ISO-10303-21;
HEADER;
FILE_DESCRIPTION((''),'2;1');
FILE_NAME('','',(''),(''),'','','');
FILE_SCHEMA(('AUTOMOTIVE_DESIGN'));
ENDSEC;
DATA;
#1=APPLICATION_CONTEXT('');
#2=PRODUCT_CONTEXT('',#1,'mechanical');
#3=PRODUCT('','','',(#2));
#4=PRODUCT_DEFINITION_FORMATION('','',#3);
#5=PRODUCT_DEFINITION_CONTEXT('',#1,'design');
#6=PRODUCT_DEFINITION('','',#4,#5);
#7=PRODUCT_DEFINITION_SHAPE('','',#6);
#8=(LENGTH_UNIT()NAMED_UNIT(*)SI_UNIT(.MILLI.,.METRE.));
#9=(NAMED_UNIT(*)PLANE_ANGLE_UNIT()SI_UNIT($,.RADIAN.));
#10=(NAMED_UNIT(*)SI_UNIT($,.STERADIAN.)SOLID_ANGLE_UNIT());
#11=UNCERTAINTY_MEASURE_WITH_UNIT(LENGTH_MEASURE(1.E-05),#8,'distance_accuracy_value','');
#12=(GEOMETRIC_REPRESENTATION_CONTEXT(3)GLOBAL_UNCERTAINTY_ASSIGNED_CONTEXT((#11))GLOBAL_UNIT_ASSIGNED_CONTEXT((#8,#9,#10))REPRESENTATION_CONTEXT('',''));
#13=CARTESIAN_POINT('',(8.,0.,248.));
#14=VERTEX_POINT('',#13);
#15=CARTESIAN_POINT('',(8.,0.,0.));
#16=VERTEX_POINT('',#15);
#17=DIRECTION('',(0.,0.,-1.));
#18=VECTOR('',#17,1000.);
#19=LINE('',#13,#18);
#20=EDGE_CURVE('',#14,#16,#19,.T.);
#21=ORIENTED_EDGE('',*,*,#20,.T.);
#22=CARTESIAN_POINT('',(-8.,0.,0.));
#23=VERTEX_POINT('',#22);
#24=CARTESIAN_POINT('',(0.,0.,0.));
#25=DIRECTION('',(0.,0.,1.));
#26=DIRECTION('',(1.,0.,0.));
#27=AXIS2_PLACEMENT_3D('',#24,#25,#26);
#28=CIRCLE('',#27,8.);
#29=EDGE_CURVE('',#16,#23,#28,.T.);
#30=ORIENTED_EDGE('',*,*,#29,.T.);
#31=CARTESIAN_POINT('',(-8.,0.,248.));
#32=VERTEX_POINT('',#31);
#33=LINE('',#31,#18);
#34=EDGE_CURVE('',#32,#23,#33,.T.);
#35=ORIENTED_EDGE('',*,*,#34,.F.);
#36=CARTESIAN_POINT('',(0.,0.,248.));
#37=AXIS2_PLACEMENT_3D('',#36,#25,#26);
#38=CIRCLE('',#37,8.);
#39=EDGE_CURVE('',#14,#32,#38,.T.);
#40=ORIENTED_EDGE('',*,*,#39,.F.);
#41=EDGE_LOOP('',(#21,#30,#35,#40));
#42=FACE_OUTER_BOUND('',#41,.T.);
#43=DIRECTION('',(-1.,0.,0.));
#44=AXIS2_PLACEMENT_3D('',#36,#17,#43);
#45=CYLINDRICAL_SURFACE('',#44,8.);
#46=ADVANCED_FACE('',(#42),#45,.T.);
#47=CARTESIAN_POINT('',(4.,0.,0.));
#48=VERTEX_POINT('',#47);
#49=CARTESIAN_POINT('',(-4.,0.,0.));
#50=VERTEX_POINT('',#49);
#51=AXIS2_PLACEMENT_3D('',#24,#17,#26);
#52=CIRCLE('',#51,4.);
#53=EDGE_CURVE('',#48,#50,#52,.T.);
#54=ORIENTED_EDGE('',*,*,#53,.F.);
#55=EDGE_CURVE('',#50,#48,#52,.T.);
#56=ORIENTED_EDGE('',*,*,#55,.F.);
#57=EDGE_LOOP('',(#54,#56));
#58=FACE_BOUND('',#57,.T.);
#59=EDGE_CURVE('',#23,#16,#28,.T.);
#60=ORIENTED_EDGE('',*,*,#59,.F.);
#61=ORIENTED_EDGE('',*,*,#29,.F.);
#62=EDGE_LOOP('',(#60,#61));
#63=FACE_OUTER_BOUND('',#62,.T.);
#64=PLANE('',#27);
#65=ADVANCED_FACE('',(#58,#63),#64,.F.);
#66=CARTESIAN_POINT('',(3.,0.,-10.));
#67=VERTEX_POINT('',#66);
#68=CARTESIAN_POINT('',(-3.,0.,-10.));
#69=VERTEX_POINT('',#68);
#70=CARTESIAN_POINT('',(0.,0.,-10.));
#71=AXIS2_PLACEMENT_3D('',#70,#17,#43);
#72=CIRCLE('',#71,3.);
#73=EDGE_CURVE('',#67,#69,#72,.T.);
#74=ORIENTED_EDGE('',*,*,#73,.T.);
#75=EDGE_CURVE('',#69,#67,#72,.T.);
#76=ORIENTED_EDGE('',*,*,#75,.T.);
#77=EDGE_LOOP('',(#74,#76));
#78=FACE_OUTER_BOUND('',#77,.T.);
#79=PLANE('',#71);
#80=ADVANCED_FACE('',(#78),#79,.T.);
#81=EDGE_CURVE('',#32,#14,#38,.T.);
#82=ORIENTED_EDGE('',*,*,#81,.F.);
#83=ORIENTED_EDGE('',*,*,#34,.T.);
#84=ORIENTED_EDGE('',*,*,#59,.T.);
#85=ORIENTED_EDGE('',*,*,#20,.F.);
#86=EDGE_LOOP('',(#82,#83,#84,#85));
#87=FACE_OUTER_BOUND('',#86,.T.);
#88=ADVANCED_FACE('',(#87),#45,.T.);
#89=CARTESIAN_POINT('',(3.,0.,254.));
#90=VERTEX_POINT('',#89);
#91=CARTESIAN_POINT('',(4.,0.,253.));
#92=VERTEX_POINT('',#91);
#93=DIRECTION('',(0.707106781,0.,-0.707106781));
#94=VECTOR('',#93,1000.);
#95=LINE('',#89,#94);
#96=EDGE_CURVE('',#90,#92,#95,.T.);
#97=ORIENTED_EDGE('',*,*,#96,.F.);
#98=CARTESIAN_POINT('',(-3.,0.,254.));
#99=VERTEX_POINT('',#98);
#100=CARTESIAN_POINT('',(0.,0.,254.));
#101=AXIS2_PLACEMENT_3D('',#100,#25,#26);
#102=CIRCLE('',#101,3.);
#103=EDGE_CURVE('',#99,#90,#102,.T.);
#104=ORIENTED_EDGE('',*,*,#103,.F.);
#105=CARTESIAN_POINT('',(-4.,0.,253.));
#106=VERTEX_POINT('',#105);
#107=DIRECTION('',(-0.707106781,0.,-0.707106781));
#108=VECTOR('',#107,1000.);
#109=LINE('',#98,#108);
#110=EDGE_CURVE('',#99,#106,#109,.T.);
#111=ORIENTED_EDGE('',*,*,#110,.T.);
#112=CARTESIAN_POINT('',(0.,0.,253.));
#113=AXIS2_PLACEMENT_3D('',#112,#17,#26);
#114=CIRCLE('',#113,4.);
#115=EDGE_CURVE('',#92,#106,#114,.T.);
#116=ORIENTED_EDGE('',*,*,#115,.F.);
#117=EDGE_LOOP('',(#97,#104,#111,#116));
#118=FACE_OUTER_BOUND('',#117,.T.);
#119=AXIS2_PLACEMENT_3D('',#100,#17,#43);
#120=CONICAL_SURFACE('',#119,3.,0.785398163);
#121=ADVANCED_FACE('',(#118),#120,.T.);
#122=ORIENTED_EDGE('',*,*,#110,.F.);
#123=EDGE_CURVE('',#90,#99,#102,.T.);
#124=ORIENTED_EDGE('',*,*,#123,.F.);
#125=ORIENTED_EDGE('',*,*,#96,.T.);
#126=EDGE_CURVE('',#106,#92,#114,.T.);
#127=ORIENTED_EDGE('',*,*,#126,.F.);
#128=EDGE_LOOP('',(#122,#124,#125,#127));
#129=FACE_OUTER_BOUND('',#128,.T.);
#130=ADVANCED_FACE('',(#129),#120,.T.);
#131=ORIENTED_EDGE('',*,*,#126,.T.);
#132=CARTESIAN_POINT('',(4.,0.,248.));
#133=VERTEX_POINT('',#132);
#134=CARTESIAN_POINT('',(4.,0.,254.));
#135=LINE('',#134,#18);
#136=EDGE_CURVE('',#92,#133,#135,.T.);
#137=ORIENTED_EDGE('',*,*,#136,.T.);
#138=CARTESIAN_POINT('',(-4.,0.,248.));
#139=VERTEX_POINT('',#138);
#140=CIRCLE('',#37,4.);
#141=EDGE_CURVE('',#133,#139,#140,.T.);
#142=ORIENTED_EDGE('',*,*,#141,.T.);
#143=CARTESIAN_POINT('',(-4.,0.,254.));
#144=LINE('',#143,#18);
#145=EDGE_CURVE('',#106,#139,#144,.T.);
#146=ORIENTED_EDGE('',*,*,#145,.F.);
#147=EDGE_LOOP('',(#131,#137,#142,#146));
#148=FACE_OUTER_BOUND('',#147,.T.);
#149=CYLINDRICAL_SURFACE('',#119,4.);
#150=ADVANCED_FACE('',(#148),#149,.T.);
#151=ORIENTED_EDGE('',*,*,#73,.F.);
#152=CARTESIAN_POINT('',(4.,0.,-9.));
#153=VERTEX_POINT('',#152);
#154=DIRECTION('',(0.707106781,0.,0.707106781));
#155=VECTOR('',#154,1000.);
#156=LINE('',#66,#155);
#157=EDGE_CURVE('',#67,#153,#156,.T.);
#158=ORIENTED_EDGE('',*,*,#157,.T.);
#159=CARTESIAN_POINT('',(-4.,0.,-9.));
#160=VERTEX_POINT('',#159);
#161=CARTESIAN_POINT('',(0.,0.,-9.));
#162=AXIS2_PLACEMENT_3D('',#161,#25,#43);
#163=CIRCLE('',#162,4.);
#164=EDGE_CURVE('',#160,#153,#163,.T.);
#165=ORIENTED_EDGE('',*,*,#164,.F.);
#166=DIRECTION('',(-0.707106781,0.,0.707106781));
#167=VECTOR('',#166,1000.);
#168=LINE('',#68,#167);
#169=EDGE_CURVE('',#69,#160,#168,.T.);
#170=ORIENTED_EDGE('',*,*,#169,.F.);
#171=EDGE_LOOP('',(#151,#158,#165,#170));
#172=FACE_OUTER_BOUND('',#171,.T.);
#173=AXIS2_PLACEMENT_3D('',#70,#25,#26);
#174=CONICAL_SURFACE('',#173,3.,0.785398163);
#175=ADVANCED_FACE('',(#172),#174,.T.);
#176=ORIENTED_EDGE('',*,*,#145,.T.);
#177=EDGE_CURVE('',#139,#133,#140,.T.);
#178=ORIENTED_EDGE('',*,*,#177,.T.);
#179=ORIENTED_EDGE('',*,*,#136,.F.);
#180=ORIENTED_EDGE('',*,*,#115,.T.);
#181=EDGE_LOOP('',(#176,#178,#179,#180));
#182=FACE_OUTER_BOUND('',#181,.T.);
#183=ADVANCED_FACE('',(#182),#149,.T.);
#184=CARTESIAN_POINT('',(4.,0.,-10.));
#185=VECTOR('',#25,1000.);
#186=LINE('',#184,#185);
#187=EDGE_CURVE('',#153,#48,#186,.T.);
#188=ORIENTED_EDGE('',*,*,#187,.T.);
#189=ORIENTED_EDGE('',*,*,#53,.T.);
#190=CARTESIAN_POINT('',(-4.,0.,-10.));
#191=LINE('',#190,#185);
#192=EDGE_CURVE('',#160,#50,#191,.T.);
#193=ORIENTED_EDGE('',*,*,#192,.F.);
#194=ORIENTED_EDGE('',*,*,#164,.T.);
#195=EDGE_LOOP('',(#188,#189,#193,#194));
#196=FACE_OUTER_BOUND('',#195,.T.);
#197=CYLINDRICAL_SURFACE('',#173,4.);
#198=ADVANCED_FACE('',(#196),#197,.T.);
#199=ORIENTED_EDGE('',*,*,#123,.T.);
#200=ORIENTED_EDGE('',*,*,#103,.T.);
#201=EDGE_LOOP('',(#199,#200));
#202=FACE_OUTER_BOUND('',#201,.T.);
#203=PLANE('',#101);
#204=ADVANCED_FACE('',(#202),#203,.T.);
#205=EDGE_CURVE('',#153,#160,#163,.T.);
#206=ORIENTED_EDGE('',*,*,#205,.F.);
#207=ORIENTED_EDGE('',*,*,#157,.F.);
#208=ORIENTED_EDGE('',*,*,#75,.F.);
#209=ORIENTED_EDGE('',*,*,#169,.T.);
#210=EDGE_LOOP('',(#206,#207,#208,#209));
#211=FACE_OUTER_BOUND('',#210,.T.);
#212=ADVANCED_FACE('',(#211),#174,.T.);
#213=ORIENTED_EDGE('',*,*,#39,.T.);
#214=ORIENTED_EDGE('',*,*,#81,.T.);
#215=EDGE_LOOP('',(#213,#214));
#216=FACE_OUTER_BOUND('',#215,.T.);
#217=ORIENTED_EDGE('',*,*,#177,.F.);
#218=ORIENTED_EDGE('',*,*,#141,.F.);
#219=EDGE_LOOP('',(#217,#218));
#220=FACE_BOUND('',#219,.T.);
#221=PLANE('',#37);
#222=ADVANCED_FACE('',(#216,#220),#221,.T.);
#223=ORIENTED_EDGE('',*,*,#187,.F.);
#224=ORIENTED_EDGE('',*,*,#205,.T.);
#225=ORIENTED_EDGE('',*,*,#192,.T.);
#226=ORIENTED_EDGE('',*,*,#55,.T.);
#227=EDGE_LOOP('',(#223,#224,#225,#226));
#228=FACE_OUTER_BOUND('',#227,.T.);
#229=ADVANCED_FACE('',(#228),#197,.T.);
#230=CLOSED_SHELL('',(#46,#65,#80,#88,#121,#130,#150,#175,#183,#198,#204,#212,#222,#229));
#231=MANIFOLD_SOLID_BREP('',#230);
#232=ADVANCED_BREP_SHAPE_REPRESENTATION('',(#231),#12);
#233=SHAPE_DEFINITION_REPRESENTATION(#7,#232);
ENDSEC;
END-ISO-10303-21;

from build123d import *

# Parameters (mm, degrees)
SKETCH1_R           = 8
BOSS_EXTRUDE1_DEPTH = 248
SKETCH2_R           = 4
BOSS_EXTRUDE2_DEPTH = 10
BOSS_EXTRUDE3_START = 6
SKETCH3_R           = 4
BOSS_EXTRUDE3_DEPTH = 6
CHAMFER1_SIZE       = 1


with BuildPart() as part:
    # Sketch1 → Boss-Extrude1 (new body)
    with BuildSketch(Plane.XY):
        Circle(SKETCH1_R)
    extrude(amount=BOSS_EXTRUDE1_DEPTH)

    # Sketch2 → Boss-Extrude2 (add)
    with BuildSketch(Plane(origin=(0, 0, 0), x_dir=(-1, 0, 0), z_dir=(0, 0, -1))):
        with Locations(Location((0, 0, 0), (0, 0, 180))):
            Circle(SKETCH2_R)
    extrude(amount=BOSS_EXTRUDE2_DEPTH)

    # Sketch3 → Boss-Extrude3 (add)
    with BuildSketch(Plane.XY.offset(248).offset(BOSS_EXTRUDE3_START)):
        Circle(SKETCH3_R)
    extrude(amount=-BOSS_EXTRUDE3_DEPTH)

    # Chamfer1
    chamfer1_edges = [part.edges().sort_by_distance(p)[0] for p in [
        (-4, 0, 254),
        (-4, 0, -10),
    ]]
    chamfer(chamfer1_edges, length=CHAMFER1_SIZE)


solid = part.part
